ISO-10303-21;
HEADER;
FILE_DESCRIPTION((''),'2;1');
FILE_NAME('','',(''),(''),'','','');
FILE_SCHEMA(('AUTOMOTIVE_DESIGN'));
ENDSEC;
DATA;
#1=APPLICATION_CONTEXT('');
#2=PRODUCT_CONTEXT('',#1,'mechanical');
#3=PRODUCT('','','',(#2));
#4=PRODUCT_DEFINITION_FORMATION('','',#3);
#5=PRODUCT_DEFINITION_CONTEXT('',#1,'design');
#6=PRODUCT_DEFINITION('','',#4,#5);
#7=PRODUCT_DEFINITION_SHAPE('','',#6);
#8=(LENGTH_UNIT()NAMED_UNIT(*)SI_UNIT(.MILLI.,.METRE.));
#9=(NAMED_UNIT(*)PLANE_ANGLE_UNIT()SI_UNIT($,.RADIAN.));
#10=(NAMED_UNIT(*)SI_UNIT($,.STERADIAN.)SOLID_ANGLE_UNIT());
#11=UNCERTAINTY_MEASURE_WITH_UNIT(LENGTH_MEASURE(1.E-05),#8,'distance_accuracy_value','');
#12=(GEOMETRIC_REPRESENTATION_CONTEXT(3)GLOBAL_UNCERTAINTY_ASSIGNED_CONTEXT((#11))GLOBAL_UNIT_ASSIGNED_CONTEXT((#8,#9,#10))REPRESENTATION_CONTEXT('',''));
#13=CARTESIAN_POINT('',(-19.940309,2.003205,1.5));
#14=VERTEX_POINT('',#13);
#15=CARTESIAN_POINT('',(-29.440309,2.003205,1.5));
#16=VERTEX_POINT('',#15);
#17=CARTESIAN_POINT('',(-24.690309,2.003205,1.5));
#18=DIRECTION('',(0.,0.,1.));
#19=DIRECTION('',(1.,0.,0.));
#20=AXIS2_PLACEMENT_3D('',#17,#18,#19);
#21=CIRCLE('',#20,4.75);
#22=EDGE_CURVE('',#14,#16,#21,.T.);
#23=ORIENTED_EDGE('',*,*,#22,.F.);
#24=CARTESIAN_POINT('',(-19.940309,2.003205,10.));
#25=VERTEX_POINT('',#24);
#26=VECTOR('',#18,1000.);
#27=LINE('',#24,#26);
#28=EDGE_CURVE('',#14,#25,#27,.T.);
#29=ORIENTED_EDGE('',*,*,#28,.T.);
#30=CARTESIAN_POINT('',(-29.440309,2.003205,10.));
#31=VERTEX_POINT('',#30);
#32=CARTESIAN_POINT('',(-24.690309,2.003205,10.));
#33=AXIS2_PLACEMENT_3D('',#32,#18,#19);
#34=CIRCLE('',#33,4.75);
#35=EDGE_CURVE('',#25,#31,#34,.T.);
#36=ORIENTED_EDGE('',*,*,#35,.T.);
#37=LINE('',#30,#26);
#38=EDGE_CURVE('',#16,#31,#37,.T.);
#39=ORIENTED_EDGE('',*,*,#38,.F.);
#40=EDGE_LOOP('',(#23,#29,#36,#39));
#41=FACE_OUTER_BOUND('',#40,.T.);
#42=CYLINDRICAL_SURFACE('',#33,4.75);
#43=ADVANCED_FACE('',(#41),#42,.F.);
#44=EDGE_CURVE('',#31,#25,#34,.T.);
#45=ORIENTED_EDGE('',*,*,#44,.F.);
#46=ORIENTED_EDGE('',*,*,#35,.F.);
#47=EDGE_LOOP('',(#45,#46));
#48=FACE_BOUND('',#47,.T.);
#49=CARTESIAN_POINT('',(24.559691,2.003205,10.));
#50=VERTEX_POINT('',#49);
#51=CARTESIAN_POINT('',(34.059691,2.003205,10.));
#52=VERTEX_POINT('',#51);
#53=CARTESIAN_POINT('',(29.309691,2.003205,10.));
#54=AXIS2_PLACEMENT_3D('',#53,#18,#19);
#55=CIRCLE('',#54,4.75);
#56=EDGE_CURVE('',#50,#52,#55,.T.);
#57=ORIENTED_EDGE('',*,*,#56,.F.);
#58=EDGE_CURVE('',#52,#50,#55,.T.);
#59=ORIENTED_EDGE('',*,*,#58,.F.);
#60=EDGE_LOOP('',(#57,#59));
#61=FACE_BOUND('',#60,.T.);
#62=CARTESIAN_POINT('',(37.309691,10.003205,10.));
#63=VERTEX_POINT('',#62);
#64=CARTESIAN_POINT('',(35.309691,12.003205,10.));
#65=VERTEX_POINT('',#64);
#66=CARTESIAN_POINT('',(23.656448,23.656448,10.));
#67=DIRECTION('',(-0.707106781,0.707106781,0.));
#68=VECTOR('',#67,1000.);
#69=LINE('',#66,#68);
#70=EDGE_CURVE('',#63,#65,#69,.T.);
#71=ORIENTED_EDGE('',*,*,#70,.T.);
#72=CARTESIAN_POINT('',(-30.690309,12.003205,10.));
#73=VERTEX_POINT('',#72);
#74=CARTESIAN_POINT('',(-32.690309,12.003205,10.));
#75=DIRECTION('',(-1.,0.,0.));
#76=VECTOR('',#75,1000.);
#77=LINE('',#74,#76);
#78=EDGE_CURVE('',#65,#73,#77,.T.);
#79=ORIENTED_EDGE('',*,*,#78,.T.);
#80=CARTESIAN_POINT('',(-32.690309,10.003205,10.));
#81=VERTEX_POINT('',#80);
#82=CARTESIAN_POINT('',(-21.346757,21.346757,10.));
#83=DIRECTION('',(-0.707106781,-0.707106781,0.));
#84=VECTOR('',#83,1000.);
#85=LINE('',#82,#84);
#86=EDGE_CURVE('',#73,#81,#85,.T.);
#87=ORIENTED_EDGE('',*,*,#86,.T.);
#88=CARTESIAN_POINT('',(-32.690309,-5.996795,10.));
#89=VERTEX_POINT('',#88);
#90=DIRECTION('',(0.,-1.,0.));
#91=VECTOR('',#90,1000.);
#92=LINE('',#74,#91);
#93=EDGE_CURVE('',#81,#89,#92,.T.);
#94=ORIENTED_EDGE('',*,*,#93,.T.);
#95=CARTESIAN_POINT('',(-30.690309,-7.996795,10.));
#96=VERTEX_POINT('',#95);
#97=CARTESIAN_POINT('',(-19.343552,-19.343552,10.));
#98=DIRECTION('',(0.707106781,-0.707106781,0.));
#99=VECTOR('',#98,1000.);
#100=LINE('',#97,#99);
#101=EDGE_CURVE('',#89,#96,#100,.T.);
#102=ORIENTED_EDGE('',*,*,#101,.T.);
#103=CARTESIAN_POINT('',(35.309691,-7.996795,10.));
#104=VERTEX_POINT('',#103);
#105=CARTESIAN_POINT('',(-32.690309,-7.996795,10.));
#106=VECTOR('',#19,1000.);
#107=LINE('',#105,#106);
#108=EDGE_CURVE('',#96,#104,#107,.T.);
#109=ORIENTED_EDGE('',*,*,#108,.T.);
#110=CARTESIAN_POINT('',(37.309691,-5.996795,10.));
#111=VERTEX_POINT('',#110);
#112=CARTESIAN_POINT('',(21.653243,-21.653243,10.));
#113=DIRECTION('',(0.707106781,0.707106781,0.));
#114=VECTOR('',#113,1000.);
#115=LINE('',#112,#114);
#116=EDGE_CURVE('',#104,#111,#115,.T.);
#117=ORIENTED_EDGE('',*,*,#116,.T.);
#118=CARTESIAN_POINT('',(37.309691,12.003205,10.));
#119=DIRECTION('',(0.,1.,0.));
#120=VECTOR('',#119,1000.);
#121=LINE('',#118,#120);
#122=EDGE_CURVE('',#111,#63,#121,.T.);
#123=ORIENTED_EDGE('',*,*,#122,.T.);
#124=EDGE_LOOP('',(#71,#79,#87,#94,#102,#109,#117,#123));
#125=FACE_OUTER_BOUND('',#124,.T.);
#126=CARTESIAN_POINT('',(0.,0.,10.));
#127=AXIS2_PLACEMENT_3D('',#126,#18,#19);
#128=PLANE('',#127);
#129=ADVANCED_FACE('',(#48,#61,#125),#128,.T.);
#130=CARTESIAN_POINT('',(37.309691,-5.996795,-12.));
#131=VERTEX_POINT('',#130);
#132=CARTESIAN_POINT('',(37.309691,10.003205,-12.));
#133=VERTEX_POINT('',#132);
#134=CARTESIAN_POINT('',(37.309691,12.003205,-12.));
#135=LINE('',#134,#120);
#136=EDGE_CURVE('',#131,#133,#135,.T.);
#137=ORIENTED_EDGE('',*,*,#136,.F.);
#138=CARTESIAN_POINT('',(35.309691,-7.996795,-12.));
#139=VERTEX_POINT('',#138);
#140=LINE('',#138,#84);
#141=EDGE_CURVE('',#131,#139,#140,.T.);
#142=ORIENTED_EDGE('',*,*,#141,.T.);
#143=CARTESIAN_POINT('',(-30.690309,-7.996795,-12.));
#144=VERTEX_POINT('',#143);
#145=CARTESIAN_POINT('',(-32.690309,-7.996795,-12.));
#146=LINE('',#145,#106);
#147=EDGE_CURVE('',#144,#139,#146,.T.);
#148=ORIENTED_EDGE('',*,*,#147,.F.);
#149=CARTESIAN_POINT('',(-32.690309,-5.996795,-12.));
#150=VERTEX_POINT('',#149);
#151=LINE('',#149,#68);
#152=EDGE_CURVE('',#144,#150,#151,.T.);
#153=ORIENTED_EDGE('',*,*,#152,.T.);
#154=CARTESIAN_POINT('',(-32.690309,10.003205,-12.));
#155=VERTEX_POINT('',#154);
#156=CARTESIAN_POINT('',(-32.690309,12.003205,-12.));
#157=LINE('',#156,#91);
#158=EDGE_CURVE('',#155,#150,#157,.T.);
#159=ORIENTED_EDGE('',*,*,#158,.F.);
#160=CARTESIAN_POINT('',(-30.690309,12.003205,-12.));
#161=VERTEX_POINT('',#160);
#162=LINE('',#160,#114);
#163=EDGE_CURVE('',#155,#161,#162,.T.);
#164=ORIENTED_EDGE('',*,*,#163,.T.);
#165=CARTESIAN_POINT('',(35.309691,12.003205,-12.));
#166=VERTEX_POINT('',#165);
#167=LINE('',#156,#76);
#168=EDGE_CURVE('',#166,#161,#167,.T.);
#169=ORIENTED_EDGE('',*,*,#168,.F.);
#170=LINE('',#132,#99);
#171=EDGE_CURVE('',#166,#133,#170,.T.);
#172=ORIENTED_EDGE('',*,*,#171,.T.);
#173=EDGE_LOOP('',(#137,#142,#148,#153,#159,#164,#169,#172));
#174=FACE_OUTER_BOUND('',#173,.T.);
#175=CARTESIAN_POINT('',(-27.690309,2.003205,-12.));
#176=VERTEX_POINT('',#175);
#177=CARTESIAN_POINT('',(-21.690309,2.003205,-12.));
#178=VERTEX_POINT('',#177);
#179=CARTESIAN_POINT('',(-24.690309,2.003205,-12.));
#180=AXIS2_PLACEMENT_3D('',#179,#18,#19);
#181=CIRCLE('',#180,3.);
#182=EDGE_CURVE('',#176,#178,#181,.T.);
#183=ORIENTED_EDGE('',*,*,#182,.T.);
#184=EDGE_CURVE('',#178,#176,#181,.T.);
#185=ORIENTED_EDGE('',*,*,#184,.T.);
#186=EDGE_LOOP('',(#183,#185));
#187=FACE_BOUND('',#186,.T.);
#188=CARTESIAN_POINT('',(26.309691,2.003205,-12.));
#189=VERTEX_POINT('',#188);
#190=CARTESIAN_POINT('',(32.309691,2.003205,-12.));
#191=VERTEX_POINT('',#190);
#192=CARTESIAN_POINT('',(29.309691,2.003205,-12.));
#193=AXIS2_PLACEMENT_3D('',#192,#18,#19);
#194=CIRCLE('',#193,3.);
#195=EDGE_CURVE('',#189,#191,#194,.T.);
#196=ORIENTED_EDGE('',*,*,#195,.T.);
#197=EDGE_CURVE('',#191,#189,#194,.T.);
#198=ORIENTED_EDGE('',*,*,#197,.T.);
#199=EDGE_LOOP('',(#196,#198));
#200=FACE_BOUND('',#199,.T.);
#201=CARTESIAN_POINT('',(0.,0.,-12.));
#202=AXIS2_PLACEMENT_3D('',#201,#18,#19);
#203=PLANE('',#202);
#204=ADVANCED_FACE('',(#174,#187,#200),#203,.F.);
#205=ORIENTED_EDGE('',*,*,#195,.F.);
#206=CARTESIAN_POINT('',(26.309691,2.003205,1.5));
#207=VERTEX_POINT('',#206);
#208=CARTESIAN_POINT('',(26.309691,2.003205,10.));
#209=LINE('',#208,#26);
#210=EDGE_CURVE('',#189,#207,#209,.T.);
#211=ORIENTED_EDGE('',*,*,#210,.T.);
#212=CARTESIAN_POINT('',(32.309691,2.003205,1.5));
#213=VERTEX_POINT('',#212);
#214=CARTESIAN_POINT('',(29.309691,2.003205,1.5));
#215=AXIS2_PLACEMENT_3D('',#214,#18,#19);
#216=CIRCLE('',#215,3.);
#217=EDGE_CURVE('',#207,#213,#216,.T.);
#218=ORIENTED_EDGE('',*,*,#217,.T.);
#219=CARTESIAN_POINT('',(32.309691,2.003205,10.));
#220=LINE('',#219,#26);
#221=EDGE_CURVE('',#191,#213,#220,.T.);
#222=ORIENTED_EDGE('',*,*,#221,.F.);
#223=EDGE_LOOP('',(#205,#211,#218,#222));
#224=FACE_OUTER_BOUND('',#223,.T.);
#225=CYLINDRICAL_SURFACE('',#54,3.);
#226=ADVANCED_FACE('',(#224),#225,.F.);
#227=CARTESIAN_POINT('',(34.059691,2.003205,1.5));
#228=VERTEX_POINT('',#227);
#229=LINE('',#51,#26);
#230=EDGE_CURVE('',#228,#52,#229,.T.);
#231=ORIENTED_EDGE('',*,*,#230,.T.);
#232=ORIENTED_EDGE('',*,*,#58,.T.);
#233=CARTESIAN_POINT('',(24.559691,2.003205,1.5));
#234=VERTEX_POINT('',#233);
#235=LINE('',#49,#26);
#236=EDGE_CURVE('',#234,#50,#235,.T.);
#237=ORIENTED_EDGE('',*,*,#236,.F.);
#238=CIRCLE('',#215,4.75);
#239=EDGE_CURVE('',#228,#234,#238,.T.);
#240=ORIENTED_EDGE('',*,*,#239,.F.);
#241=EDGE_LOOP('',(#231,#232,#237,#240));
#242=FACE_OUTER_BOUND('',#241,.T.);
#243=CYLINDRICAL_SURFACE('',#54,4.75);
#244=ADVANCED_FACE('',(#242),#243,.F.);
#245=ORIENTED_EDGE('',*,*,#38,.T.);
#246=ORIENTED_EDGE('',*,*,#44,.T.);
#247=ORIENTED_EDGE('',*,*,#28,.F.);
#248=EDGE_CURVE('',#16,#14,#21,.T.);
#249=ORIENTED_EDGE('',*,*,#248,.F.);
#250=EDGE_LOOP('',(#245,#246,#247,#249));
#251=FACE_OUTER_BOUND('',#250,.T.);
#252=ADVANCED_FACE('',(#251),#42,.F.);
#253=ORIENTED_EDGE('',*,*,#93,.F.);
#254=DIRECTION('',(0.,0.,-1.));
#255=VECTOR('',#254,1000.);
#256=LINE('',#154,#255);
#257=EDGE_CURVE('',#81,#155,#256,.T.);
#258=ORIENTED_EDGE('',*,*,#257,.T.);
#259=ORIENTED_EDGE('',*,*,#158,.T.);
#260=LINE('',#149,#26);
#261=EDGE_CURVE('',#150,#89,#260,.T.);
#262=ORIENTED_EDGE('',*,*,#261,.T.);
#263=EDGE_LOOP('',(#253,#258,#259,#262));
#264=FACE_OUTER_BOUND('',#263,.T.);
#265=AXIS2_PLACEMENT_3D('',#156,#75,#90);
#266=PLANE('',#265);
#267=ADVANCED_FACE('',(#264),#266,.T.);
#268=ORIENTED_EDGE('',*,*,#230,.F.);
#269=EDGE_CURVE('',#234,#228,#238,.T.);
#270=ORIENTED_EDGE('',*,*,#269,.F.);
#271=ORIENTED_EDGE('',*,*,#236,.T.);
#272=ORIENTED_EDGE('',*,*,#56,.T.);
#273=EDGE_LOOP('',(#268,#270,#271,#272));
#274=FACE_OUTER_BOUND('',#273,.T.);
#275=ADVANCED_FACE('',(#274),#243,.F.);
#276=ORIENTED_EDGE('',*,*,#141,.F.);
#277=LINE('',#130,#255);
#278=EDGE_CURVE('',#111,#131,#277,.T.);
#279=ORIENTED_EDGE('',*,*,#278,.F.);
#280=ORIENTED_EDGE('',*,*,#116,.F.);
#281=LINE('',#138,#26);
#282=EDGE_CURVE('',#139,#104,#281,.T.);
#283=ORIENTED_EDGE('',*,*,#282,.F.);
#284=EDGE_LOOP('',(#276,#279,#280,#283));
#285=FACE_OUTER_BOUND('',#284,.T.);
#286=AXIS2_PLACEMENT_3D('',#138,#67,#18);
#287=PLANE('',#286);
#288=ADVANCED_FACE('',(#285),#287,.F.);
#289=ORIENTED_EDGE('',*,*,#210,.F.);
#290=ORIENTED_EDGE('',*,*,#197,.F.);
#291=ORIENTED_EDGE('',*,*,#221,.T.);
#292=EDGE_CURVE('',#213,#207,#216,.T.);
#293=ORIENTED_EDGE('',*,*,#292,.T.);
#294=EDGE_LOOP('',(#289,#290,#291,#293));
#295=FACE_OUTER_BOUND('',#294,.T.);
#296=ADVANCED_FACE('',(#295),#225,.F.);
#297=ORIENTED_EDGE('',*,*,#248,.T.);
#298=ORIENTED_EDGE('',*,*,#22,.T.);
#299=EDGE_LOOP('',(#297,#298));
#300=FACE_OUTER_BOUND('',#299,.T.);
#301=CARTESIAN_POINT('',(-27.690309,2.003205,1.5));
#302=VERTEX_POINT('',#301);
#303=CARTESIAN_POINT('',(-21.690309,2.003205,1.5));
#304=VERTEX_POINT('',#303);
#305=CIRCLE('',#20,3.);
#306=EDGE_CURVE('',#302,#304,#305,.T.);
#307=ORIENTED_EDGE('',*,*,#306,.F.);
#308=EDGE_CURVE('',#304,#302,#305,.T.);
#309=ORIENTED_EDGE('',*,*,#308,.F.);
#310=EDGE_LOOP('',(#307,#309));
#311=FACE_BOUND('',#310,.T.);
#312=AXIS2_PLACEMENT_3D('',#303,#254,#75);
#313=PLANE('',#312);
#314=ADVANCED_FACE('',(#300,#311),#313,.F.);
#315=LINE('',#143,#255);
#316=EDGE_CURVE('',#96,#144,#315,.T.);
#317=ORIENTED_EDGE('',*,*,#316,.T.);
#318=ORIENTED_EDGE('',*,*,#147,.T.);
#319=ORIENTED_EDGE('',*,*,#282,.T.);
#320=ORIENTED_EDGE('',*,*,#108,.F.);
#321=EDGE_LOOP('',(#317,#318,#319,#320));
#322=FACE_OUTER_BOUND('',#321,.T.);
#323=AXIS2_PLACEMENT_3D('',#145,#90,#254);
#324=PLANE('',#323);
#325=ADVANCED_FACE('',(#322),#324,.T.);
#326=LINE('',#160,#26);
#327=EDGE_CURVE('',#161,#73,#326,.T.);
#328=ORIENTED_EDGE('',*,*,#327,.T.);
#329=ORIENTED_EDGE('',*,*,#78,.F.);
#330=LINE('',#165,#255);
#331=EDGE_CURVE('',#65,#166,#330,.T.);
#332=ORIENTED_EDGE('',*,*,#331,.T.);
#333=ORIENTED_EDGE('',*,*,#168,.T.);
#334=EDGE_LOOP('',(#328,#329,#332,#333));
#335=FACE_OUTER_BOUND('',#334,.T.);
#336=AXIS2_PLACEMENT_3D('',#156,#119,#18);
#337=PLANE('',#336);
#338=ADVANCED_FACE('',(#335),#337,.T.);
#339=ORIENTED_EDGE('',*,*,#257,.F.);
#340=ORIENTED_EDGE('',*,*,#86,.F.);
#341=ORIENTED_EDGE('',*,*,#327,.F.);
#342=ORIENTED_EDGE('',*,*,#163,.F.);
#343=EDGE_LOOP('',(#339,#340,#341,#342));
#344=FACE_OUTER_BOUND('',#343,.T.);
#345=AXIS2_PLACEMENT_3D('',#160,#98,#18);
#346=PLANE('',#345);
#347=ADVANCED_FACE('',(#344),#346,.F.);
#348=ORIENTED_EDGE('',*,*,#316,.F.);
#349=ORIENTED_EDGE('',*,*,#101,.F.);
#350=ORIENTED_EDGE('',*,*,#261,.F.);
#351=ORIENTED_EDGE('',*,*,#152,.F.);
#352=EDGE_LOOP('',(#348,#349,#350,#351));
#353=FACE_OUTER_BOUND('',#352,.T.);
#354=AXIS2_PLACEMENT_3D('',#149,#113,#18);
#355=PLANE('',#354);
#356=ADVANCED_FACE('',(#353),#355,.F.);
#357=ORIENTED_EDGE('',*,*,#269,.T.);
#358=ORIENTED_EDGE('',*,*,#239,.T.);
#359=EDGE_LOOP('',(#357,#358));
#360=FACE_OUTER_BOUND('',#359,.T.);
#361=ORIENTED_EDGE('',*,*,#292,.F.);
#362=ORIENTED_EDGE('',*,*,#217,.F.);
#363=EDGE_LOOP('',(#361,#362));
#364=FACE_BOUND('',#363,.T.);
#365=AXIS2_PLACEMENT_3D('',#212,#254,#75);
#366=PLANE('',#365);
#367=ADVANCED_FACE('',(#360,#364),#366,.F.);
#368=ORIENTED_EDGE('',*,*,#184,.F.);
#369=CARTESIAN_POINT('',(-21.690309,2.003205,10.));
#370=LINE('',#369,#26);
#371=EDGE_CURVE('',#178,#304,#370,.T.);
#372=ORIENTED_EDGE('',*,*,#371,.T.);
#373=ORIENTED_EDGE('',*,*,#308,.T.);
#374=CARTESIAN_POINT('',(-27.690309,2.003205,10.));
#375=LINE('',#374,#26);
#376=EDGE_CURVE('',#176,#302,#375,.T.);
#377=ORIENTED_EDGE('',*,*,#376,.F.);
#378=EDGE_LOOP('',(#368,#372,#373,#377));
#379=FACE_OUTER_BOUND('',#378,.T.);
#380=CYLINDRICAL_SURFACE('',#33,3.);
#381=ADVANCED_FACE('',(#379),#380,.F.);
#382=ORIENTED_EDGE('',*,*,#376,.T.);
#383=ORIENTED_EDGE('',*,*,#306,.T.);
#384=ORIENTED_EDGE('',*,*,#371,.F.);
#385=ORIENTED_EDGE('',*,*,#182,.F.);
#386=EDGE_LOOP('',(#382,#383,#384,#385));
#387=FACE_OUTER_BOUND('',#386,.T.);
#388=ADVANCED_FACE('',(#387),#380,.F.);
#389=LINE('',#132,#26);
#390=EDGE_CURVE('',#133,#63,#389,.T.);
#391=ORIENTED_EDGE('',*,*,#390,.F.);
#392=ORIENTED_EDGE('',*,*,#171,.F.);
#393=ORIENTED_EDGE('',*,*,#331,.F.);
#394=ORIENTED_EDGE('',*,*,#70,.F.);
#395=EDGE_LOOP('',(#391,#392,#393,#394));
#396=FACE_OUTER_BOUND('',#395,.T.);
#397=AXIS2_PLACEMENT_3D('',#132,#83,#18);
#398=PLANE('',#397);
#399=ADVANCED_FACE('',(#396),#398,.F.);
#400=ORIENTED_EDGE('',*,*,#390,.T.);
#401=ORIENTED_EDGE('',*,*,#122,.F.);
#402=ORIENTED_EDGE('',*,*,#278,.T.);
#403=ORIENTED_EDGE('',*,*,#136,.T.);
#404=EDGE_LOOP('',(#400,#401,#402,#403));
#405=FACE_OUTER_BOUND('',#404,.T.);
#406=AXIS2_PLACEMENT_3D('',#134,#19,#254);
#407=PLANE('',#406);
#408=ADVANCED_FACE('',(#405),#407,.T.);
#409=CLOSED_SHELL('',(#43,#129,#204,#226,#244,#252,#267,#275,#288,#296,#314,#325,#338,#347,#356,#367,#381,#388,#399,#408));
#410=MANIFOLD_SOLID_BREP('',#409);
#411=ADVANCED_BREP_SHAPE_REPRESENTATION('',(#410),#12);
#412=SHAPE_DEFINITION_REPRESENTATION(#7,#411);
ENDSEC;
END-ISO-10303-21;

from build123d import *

# Parameters (mm, degrees)
BOSS_EXTRUDE1_DEPTH      = 10
BOSS_EXTRUDE1_DEPTH_BACK = 12
SKETCH1_W                = 70
SKETCH1_H                = 20
SKETCH1_R                = 2.187999439
SKETCH1_R_2              = 2.181063018
HOLE1_D                  = 6
HOLE1_CBORE_D            = 9.5
HOLE1_CBORE_DEPTH        = 8.5
CHAMFER1_SIZE            = 2


with BuildPart() as part:
    # Sketch1 → Boss-Extrude1 (new, two sides: drawn at the far end of the back side and taken through both)
    with BuildSketch(Plane.XY.offset(-BOSS_EXTRUDE1_DEPTH_BACK)):
        with Locations((2.309691162, 2.003205128)):
            Rectangle(SKETCH1_W, SKETCH1_H)
        with Locations((-24.690308838, 2.003205128)):
            Circle(SKETCH1_R, mode=Mode.SUBTRACT)
        with Locations((29.309691162, 2.003205128)):
            Circle(SKETCH1_R_2, mode=Mode.SUBTRACT)
    extrude(amount=BOSS_EXTRUDE1_DEPTH + BOSS_EXTRUDE1_DEPTH_BACK)

    # Hole1 (through all)
    with Locations(Plane.XY.offset(10)):
        with Locations((-24.690308838, 2.003205128), (29.309691162, 2.003205128)):
            CounterBoreHole(HOLE1_D / 2, HOLE1_CBORE_D / 2, HOLE1_CBORE_DEPTH)

    # Chamfer1
    chamfer1_edges = [part.edges().sort_by_distance(p)[0] for p in [
        (-32.690308838, 12.003205128, -1),
        (37.309691162, 12.003205128, -1),
        (37.309691162, -7.996794872, -1),
        (-32.690308838, -7.996794872, -1),
    ]]
    chamfer(chamfer1_edges, length=CHAMFER1_SIZE)


solid = part.part
